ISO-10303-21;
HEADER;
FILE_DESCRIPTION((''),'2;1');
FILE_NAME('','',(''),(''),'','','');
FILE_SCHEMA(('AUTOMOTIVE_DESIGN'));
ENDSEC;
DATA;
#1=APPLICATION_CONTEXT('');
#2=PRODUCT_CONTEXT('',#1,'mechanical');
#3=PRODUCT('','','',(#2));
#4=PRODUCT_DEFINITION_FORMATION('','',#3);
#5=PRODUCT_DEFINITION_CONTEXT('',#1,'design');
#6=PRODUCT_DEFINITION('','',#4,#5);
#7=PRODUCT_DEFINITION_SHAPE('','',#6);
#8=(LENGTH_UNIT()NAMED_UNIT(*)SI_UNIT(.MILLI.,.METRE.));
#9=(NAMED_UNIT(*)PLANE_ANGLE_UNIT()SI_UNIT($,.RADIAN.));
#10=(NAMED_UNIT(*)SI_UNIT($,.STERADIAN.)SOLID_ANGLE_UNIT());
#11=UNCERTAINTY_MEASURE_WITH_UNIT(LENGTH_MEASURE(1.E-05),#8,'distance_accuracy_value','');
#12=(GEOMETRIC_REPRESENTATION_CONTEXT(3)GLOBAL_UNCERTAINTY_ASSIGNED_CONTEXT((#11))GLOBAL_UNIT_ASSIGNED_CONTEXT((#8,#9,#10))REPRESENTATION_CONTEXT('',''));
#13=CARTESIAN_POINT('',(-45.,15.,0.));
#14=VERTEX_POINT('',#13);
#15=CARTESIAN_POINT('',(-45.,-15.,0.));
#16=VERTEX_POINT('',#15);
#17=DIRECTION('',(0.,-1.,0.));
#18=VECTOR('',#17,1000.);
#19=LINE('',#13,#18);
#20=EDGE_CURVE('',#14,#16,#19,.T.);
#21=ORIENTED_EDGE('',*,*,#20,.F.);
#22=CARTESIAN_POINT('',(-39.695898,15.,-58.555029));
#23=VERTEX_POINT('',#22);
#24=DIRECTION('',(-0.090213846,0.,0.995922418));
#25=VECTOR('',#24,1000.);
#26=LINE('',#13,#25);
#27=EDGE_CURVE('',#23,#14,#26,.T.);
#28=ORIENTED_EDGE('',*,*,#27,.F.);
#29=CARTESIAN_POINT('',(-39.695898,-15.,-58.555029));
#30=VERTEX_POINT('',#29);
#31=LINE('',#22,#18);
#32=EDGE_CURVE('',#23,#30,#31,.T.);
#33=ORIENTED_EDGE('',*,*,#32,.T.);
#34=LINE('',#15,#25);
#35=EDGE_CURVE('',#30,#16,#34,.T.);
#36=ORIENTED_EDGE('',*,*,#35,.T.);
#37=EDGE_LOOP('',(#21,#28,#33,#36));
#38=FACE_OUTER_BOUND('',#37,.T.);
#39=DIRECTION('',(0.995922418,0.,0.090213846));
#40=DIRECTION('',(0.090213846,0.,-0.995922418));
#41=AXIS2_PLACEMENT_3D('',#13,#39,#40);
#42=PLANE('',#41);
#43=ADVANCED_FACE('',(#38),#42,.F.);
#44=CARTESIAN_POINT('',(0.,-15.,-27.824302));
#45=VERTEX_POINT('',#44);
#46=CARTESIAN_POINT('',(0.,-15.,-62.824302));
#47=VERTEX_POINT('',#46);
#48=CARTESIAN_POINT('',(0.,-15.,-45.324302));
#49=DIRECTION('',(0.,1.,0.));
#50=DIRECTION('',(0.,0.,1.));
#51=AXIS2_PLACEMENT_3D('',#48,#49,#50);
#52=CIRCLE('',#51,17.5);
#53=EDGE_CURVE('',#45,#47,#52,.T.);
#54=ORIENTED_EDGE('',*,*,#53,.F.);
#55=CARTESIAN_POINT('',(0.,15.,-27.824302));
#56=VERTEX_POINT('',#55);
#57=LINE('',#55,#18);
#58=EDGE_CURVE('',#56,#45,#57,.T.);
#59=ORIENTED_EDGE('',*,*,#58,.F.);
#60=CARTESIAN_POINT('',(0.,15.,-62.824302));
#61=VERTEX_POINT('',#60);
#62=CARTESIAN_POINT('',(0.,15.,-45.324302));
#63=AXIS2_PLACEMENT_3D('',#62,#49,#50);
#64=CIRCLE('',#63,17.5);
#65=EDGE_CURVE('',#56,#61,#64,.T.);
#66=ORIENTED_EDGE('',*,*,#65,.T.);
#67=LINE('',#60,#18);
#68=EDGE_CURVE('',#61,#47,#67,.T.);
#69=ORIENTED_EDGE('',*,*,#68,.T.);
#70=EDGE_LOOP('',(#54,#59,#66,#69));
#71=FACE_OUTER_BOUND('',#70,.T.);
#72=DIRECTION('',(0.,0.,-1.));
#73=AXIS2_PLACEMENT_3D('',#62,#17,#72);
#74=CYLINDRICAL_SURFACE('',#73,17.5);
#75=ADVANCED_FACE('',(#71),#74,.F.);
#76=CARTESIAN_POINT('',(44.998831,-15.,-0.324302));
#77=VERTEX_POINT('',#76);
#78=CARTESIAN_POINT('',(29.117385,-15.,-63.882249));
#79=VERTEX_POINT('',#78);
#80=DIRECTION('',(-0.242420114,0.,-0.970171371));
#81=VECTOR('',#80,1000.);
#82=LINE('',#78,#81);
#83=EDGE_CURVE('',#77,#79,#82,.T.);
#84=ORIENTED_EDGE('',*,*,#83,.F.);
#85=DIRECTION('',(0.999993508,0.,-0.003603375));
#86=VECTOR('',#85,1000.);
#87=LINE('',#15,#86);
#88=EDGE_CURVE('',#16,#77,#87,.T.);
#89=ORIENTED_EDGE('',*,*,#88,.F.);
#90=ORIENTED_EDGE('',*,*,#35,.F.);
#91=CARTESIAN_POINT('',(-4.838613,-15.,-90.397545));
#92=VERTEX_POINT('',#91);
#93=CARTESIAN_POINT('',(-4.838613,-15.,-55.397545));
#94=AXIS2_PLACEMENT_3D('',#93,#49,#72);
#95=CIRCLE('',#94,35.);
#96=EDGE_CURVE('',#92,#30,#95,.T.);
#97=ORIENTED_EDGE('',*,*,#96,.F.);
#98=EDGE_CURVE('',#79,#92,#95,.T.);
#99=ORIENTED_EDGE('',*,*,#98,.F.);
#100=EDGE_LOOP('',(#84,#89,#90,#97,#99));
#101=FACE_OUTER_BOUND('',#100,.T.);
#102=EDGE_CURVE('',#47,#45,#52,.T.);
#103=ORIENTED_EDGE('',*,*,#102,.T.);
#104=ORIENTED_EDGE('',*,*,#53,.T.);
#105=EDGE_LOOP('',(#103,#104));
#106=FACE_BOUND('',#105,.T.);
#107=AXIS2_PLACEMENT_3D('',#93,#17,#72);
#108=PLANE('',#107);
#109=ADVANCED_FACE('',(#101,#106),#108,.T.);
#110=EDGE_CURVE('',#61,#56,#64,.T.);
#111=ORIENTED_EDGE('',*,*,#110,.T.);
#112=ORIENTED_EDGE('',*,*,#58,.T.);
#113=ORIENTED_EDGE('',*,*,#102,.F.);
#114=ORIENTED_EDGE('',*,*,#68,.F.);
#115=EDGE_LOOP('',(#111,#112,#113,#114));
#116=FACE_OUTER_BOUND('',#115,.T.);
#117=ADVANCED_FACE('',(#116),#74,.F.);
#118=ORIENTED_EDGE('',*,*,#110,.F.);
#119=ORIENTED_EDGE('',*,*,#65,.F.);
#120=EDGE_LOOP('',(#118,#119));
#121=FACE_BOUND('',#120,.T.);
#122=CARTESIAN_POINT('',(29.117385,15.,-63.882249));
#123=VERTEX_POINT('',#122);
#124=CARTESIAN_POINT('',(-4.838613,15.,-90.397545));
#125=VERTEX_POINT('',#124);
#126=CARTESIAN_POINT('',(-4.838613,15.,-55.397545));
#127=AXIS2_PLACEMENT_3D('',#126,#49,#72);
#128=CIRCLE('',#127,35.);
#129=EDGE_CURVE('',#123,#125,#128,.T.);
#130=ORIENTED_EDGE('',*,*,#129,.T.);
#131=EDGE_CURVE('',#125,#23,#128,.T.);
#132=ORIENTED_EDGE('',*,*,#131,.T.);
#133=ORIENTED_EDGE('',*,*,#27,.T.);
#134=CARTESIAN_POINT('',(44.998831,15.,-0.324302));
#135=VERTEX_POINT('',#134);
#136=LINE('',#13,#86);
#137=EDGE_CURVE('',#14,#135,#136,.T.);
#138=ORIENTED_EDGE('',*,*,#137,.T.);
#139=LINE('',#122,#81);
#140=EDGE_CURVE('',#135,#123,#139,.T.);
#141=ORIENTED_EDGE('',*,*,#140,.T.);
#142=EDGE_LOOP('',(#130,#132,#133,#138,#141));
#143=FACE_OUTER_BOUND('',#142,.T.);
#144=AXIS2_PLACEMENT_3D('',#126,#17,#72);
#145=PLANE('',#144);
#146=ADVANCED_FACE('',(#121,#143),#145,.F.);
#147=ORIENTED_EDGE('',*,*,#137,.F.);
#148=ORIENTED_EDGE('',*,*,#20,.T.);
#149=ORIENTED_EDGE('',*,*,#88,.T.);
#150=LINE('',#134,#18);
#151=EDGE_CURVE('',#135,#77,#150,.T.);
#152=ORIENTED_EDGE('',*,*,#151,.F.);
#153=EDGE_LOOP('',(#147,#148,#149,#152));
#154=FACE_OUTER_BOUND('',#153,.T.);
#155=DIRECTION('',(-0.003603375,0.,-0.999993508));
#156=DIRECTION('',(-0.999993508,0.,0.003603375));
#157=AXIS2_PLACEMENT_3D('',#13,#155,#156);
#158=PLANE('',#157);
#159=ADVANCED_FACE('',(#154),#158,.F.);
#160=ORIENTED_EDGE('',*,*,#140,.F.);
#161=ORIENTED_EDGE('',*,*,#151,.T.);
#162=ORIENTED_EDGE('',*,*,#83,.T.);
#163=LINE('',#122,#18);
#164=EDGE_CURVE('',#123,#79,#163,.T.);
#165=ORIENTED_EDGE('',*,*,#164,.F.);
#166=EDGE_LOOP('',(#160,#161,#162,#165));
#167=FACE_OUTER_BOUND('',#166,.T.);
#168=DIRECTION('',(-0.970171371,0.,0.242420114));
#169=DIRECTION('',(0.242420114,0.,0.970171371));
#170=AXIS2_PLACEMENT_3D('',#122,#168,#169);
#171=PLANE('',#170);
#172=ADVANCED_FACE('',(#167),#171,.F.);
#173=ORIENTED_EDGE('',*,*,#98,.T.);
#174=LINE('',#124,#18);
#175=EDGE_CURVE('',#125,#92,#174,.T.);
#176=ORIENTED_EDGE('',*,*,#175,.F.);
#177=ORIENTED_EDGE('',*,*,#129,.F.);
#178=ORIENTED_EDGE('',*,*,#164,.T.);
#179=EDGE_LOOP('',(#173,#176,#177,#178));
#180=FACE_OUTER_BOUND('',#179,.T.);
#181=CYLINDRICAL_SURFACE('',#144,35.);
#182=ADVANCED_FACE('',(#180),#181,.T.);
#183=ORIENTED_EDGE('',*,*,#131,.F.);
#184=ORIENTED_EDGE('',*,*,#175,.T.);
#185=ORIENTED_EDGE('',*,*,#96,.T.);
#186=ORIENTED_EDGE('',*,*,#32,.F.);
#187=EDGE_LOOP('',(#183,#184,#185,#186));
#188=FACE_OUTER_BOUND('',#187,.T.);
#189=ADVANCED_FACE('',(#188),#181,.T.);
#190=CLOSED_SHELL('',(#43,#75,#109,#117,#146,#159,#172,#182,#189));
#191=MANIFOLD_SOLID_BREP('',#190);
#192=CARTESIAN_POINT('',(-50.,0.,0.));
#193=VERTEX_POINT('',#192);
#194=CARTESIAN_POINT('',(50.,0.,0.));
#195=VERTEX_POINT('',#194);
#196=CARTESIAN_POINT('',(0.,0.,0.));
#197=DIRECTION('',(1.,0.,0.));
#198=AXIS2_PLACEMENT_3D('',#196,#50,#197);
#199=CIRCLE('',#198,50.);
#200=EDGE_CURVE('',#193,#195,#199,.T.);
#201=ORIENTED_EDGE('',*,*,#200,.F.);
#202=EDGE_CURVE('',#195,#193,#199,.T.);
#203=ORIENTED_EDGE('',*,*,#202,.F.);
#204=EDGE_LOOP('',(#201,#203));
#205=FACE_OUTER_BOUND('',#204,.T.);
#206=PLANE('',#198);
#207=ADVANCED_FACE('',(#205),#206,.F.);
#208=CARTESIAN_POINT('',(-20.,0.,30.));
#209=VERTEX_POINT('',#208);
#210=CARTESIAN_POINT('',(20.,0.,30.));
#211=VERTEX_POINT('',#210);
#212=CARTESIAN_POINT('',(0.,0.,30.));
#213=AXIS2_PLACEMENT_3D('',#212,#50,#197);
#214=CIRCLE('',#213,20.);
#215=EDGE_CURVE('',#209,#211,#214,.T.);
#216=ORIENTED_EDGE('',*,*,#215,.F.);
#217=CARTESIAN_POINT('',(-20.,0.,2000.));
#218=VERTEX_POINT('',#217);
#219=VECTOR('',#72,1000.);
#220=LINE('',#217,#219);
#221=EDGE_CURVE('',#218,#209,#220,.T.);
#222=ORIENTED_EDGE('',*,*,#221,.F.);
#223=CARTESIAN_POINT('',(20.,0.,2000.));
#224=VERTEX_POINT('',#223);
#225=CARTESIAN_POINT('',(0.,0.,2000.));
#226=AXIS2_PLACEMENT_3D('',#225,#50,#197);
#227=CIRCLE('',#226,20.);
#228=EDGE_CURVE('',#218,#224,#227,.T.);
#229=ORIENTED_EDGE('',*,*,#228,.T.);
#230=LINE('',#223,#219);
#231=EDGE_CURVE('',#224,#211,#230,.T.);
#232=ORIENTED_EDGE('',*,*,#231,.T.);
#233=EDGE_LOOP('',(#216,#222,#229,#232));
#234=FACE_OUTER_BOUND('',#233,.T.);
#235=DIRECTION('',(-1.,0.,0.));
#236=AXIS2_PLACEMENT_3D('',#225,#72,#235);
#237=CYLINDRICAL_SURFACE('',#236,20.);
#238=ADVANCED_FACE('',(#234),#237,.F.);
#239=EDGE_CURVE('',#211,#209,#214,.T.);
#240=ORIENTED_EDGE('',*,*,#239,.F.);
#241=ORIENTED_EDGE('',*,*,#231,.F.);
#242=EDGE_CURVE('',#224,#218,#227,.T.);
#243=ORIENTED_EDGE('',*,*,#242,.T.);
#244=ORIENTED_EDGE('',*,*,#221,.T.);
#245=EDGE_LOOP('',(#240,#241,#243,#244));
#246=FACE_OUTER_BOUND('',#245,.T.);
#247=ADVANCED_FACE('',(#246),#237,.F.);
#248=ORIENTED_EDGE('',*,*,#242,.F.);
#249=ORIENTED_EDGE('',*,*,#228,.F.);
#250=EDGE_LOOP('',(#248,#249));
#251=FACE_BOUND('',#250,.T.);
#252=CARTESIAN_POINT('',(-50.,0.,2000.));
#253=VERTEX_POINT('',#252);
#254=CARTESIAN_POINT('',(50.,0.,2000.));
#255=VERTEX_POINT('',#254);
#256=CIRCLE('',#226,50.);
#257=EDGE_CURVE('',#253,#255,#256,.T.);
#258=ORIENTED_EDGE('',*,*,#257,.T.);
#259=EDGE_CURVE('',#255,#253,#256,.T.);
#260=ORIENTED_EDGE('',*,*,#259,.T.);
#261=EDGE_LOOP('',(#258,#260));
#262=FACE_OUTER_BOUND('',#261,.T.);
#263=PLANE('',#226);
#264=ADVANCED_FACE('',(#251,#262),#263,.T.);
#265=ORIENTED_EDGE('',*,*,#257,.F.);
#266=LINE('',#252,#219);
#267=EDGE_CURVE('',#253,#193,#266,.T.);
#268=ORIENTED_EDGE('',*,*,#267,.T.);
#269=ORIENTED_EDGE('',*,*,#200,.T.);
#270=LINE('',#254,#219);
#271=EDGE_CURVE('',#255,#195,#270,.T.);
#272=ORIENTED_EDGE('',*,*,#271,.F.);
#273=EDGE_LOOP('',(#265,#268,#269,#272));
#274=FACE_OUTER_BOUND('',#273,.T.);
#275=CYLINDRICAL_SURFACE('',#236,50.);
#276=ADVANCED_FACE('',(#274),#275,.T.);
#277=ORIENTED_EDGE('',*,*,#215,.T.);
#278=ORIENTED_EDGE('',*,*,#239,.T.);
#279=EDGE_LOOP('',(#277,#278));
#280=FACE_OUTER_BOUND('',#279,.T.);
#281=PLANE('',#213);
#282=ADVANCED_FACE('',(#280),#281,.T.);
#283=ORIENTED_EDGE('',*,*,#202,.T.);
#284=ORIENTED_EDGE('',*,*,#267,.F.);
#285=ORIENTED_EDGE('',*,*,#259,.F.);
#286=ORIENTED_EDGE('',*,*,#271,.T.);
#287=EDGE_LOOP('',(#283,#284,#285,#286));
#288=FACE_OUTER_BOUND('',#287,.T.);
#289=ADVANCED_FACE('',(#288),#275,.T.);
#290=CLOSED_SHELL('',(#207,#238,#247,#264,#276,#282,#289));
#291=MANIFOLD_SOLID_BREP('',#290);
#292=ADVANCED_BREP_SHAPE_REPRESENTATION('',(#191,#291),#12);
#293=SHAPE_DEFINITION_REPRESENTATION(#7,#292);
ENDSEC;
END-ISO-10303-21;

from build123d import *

# Parameters (mm, degrees)
TUBE_PROFILE_100_R     = 50
TUBE_100X2000_DEPTH    = 2000
TUBE_SHELL_30_WALL_T   = -30
EYE_LUG_PROFILE_R      = 17.5
EYE_LUG_30_THICK_DEPTH = 15


with BuildPart() as part:
    # Tube Profile Ø100 → Tube Ø100x2000 (new body)
    with BuildSketch(Plane.XY):
        Circle(TUBE_PROFILE_100_R)
    extrude(amount=TUBE_100X2000_DEPTH)

    # Tube Shell 30 Wall
    tube_shell_30_wall_openings = [part.faces().sort_by_distance(p)[0] for p in [
        (0, 0, 2000),
    ]]
    offset(amount=TUBE_SHELL_30_WALL_T, openings=tube_shell_30_wall_openings, kind=Kind.INTERSECTION)


with BuildPart() as body_2:
    # Eye Lug Profile → Eye Lug 30 Thick (new, symmetric)
    with BuildSketch(Plane(origin=(0, 0, 0), x_dir=(1, 0, 0), z_dir=(0, 1, 0))):
        with BuildLine():
            Line((-45, 0), (-39.695897674, 58.555029213))
            ThreePointArc((-39.695897674, 58.555029213), (-7.540074868, 90.293133194), (29.117384917, 63.882248566))
            Line((29.117384917, 63.882248566), (44.998831412, 0.324301638))
            Line((44.998831412, 0.324301638), (-45, 0))
        make_face()
        with Locations(Location((0, 45.324301638, 0), (0, 0, 270))):
            Circle(EYE_LUG_PROFILE_R, mode=Mode.SUBTRACT)
    extrude(amount=EYE_LUG_30_THICK_DEPTH, both=True)


solid = Compound([part.part, body_2.part])
